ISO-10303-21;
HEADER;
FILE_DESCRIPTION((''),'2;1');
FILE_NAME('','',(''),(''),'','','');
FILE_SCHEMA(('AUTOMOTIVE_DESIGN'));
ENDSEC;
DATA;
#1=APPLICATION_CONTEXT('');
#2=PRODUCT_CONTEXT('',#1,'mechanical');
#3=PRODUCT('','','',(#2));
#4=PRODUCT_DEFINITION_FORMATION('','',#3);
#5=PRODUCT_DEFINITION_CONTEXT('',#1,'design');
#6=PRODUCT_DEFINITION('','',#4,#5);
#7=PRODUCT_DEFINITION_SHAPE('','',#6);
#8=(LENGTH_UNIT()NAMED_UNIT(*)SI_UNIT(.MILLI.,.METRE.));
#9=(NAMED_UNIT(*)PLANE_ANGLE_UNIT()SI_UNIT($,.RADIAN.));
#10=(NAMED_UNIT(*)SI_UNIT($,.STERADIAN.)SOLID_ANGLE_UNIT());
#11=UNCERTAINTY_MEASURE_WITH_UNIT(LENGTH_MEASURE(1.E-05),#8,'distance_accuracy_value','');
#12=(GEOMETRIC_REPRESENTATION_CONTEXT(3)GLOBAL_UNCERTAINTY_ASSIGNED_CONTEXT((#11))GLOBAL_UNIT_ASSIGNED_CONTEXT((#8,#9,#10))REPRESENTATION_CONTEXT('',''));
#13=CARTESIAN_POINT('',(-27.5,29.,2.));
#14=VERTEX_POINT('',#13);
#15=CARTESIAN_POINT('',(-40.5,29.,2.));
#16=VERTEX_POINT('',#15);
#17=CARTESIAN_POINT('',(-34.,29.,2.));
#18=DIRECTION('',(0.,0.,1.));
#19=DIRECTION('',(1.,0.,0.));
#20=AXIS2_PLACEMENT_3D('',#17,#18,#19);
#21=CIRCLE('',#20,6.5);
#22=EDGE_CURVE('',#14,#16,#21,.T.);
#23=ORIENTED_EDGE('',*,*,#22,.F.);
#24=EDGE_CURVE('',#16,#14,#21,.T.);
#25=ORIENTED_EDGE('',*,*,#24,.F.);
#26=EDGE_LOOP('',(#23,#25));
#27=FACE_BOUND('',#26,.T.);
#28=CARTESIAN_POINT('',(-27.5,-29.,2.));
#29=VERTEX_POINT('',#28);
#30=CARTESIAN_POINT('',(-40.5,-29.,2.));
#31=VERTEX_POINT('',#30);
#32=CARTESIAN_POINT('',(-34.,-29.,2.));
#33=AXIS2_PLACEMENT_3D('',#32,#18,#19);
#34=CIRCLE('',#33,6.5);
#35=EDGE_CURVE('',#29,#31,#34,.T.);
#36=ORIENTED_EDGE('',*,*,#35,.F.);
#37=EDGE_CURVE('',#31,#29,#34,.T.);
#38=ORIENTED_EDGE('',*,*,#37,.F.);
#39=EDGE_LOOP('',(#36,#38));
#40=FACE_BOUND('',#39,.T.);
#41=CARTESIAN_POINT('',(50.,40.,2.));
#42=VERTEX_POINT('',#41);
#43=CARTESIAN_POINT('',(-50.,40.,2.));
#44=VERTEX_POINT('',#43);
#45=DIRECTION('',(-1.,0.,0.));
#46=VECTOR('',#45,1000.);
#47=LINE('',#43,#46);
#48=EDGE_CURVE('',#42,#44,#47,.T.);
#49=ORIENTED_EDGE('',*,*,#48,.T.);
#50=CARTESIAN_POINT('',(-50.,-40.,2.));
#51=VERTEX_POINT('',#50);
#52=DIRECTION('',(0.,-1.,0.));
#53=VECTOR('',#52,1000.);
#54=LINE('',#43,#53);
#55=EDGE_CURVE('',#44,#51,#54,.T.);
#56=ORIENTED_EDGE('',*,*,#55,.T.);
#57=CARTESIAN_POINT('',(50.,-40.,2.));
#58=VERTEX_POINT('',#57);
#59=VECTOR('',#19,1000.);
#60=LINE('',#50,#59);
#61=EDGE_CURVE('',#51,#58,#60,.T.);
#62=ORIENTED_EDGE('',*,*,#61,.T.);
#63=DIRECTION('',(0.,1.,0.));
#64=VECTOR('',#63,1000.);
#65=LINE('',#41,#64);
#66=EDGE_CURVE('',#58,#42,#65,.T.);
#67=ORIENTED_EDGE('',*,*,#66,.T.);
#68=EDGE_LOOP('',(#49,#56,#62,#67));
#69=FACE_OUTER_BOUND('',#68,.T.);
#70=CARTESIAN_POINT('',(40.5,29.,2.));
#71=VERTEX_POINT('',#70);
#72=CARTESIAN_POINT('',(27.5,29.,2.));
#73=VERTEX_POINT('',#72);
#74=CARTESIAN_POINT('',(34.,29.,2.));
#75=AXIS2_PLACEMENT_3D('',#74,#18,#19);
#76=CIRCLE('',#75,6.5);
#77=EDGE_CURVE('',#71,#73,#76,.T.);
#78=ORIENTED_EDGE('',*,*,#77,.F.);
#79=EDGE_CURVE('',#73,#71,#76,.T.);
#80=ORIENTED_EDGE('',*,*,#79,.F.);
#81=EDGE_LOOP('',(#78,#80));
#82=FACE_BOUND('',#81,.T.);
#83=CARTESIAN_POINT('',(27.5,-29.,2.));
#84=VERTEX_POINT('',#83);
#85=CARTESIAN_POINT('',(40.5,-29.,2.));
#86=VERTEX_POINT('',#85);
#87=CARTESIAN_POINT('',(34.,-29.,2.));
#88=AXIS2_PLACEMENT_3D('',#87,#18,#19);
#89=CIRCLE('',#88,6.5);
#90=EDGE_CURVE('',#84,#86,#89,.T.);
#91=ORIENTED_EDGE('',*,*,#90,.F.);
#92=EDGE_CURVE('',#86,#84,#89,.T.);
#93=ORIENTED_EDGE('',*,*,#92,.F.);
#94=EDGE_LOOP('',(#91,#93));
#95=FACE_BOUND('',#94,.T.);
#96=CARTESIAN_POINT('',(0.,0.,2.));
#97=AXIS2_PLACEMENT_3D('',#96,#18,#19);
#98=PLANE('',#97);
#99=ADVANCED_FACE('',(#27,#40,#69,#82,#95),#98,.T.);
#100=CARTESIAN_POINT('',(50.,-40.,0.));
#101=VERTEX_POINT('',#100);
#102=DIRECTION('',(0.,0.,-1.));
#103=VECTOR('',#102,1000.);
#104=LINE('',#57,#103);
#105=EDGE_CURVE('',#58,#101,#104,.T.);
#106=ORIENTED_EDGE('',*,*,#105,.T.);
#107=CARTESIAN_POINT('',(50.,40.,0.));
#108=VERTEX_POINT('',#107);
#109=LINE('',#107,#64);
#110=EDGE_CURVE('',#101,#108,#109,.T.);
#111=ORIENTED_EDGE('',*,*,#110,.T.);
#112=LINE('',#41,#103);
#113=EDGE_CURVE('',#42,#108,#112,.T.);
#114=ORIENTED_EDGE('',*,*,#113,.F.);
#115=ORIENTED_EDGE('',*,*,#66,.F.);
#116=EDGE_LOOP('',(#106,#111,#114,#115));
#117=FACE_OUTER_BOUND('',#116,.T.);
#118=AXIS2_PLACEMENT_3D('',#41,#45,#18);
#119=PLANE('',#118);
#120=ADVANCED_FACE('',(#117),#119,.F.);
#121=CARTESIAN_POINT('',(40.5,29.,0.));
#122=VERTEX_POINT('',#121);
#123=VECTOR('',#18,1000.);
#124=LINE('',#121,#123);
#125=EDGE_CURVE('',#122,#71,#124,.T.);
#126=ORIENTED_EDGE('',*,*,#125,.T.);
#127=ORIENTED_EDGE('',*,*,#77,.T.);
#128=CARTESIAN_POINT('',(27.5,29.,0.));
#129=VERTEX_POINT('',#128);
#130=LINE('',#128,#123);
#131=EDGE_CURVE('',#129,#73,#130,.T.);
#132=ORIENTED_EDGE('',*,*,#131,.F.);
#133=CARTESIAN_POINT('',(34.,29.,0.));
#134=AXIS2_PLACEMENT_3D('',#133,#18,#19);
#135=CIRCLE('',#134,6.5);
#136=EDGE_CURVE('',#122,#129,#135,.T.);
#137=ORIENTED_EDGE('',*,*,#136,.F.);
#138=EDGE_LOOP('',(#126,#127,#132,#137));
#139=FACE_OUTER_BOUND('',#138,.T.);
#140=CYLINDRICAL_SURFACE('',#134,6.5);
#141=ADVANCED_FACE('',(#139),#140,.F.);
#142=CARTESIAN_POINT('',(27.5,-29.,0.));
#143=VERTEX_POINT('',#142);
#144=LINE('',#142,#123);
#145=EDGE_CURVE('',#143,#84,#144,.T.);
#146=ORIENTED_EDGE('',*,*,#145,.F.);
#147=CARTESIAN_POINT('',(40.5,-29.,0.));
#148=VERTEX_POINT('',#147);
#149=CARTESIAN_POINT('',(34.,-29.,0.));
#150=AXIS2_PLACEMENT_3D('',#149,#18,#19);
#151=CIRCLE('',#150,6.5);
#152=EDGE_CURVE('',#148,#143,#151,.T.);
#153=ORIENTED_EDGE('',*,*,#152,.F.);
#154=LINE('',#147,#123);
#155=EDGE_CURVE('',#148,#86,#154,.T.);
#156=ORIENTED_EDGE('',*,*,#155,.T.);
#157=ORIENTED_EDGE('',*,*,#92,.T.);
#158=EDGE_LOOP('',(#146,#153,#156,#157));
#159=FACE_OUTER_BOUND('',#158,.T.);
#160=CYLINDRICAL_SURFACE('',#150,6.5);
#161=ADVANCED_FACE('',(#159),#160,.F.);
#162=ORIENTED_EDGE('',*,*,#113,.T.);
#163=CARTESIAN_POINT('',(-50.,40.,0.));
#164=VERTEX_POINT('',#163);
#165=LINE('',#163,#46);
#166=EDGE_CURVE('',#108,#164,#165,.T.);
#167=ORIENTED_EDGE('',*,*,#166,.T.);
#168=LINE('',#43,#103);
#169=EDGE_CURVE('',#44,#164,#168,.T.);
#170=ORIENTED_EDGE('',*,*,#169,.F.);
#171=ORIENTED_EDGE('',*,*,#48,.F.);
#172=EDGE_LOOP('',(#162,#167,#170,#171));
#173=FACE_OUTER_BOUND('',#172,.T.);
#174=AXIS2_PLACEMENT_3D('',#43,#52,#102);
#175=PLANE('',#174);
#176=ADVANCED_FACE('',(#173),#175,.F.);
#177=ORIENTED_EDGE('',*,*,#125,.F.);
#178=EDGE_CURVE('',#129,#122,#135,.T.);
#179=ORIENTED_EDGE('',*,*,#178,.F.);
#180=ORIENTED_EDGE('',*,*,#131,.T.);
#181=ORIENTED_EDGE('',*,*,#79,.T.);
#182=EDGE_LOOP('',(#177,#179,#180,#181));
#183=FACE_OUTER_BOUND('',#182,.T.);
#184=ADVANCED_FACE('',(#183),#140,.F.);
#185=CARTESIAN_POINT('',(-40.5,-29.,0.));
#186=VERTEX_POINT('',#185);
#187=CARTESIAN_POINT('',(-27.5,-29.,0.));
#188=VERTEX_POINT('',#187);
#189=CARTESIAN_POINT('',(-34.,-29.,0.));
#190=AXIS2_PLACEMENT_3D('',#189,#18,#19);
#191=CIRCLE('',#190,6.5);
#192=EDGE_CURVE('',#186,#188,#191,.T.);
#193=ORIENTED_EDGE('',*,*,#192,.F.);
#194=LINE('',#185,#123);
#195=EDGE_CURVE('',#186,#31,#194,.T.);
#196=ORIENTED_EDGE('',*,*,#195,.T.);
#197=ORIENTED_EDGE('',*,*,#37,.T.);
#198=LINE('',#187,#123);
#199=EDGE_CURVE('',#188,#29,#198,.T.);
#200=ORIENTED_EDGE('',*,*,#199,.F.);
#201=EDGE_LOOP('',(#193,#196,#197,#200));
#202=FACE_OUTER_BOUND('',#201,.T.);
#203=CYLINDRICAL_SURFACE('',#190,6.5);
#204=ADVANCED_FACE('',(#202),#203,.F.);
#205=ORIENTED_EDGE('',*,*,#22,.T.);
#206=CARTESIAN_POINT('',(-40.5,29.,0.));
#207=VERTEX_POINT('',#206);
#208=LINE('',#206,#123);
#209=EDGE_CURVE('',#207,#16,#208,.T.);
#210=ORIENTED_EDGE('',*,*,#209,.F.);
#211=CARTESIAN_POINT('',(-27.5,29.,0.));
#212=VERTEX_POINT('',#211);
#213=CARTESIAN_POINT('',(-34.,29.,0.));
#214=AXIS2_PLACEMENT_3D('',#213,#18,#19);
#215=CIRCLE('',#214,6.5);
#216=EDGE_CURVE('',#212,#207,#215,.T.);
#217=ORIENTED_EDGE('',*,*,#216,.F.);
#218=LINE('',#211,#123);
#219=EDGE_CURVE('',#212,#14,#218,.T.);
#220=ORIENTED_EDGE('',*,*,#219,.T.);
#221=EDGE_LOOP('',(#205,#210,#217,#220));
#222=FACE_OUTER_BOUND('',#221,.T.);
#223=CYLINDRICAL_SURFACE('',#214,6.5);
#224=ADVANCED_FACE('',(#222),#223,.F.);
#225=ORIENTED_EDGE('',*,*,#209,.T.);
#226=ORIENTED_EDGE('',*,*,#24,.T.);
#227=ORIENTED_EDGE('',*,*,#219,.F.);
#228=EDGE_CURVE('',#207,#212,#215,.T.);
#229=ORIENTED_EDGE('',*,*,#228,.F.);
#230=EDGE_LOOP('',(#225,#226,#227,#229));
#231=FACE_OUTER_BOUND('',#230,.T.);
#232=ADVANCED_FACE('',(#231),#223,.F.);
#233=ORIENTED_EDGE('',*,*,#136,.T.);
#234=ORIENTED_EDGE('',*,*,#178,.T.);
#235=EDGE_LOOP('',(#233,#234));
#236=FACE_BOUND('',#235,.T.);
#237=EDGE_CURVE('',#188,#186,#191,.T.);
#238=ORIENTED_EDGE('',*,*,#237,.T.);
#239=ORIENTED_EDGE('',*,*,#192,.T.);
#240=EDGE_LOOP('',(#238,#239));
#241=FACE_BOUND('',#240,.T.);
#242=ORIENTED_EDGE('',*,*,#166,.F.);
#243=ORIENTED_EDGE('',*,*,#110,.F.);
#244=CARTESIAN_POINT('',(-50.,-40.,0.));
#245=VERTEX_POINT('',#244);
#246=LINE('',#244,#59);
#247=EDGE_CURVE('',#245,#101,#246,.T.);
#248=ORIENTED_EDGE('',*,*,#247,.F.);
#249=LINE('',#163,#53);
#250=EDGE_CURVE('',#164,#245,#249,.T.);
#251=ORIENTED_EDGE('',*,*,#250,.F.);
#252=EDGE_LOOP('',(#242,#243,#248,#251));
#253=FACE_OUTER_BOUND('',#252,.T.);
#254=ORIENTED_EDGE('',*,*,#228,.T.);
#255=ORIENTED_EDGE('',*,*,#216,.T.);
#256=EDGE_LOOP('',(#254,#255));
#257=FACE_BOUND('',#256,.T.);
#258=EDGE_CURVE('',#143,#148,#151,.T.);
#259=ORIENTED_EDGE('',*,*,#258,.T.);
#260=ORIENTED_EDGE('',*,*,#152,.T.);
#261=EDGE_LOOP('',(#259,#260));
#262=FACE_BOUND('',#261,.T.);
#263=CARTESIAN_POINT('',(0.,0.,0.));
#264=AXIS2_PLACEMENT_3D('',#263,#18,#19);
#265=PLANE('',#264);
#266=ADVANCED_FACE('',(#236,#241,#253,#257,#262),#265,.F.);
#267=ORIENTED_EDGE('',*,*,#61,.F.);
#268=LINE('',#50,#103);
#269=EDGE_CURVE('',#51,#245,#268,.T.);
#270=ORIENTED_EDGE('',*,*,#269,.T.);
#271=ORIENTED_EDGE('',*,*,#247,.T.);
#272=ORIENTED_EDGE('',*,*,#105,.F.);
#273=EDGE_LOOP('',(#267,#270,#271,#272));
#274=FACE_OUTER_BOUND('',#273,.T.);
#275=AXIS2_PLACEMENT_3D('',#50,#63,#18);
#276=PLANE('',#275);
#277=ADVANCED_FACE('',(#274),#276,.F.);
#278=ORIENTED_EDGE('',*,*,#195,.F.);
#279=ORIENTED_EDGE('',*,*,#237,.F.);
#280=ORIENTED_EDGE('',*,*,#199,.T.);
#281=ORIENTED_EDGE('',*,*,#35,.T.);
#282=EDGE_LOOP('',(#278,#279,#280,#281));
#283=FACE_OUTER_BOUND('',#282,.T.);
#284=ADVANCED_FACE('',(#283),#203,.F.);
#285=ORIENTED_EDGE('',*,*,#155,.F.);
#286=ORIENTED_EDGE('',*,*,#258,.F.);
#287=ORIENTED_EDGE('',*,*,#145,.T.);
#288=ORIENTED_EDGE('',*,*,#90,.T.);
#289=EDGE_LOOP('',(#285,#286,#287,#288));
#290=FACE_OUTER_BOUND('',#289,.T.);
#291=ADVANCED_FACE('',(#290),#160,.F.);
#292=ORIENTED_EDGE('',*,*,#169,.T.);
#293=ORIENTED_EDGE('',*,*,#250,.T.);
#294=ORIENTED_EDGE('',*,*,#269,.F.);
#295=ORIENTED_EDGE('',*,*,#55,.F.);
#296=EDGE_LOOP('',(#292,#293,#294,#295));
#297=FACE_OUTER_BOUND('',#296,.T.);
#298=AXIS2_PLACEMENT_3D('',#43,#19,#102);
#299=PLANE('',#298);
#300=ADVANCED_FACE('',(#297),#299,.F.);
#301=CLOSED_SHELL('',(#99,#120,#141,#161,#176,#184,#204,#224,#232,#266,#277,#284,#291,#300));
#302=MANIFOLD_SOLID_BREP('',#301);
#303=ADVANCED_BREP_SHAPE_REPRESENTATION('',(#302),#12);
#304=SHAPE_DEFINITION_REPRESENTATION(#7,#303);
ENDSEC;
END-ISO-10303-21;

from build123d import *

# Parameters (mm, degrees)
SKETCH_1_W          = 100
SKETCH_1_H          = 80
EXTRUDE_1_DEPTH     = 2
SKETCH_2_R          = 6.5
CUT_EXTRUDE_1_DEPTH = 2


with BuildPart() as part:
    # 草图1 → 凸台-拉伸1 (new body)
    with BuildSketch(Plane.XY):
        Rectangle(SKETCH_1_W, SKETCH_1_H)
    extrude(amount=EXTRUDE_1_DEPTH)

    # 草图2 → 切除-拉伸1 (cut)
    with BuildSketch(Plane.XY.offset(2)):
        with Locations((-34, 29)):
            Circle(SKETCH_2_R)
        with Locations((34, 29)):
            Circle(SKETCH_2_R)
        with Locations((34, -29)):
            Circle(SKETCH_2_R)
        with Locations((-34, -29)):
            Circle(SKETCH_2_R)
    extrude(amount=-CUT_EXTRUDE_1_DEPTH, mode=Mode.SUBTRACT)


solid = part.part
